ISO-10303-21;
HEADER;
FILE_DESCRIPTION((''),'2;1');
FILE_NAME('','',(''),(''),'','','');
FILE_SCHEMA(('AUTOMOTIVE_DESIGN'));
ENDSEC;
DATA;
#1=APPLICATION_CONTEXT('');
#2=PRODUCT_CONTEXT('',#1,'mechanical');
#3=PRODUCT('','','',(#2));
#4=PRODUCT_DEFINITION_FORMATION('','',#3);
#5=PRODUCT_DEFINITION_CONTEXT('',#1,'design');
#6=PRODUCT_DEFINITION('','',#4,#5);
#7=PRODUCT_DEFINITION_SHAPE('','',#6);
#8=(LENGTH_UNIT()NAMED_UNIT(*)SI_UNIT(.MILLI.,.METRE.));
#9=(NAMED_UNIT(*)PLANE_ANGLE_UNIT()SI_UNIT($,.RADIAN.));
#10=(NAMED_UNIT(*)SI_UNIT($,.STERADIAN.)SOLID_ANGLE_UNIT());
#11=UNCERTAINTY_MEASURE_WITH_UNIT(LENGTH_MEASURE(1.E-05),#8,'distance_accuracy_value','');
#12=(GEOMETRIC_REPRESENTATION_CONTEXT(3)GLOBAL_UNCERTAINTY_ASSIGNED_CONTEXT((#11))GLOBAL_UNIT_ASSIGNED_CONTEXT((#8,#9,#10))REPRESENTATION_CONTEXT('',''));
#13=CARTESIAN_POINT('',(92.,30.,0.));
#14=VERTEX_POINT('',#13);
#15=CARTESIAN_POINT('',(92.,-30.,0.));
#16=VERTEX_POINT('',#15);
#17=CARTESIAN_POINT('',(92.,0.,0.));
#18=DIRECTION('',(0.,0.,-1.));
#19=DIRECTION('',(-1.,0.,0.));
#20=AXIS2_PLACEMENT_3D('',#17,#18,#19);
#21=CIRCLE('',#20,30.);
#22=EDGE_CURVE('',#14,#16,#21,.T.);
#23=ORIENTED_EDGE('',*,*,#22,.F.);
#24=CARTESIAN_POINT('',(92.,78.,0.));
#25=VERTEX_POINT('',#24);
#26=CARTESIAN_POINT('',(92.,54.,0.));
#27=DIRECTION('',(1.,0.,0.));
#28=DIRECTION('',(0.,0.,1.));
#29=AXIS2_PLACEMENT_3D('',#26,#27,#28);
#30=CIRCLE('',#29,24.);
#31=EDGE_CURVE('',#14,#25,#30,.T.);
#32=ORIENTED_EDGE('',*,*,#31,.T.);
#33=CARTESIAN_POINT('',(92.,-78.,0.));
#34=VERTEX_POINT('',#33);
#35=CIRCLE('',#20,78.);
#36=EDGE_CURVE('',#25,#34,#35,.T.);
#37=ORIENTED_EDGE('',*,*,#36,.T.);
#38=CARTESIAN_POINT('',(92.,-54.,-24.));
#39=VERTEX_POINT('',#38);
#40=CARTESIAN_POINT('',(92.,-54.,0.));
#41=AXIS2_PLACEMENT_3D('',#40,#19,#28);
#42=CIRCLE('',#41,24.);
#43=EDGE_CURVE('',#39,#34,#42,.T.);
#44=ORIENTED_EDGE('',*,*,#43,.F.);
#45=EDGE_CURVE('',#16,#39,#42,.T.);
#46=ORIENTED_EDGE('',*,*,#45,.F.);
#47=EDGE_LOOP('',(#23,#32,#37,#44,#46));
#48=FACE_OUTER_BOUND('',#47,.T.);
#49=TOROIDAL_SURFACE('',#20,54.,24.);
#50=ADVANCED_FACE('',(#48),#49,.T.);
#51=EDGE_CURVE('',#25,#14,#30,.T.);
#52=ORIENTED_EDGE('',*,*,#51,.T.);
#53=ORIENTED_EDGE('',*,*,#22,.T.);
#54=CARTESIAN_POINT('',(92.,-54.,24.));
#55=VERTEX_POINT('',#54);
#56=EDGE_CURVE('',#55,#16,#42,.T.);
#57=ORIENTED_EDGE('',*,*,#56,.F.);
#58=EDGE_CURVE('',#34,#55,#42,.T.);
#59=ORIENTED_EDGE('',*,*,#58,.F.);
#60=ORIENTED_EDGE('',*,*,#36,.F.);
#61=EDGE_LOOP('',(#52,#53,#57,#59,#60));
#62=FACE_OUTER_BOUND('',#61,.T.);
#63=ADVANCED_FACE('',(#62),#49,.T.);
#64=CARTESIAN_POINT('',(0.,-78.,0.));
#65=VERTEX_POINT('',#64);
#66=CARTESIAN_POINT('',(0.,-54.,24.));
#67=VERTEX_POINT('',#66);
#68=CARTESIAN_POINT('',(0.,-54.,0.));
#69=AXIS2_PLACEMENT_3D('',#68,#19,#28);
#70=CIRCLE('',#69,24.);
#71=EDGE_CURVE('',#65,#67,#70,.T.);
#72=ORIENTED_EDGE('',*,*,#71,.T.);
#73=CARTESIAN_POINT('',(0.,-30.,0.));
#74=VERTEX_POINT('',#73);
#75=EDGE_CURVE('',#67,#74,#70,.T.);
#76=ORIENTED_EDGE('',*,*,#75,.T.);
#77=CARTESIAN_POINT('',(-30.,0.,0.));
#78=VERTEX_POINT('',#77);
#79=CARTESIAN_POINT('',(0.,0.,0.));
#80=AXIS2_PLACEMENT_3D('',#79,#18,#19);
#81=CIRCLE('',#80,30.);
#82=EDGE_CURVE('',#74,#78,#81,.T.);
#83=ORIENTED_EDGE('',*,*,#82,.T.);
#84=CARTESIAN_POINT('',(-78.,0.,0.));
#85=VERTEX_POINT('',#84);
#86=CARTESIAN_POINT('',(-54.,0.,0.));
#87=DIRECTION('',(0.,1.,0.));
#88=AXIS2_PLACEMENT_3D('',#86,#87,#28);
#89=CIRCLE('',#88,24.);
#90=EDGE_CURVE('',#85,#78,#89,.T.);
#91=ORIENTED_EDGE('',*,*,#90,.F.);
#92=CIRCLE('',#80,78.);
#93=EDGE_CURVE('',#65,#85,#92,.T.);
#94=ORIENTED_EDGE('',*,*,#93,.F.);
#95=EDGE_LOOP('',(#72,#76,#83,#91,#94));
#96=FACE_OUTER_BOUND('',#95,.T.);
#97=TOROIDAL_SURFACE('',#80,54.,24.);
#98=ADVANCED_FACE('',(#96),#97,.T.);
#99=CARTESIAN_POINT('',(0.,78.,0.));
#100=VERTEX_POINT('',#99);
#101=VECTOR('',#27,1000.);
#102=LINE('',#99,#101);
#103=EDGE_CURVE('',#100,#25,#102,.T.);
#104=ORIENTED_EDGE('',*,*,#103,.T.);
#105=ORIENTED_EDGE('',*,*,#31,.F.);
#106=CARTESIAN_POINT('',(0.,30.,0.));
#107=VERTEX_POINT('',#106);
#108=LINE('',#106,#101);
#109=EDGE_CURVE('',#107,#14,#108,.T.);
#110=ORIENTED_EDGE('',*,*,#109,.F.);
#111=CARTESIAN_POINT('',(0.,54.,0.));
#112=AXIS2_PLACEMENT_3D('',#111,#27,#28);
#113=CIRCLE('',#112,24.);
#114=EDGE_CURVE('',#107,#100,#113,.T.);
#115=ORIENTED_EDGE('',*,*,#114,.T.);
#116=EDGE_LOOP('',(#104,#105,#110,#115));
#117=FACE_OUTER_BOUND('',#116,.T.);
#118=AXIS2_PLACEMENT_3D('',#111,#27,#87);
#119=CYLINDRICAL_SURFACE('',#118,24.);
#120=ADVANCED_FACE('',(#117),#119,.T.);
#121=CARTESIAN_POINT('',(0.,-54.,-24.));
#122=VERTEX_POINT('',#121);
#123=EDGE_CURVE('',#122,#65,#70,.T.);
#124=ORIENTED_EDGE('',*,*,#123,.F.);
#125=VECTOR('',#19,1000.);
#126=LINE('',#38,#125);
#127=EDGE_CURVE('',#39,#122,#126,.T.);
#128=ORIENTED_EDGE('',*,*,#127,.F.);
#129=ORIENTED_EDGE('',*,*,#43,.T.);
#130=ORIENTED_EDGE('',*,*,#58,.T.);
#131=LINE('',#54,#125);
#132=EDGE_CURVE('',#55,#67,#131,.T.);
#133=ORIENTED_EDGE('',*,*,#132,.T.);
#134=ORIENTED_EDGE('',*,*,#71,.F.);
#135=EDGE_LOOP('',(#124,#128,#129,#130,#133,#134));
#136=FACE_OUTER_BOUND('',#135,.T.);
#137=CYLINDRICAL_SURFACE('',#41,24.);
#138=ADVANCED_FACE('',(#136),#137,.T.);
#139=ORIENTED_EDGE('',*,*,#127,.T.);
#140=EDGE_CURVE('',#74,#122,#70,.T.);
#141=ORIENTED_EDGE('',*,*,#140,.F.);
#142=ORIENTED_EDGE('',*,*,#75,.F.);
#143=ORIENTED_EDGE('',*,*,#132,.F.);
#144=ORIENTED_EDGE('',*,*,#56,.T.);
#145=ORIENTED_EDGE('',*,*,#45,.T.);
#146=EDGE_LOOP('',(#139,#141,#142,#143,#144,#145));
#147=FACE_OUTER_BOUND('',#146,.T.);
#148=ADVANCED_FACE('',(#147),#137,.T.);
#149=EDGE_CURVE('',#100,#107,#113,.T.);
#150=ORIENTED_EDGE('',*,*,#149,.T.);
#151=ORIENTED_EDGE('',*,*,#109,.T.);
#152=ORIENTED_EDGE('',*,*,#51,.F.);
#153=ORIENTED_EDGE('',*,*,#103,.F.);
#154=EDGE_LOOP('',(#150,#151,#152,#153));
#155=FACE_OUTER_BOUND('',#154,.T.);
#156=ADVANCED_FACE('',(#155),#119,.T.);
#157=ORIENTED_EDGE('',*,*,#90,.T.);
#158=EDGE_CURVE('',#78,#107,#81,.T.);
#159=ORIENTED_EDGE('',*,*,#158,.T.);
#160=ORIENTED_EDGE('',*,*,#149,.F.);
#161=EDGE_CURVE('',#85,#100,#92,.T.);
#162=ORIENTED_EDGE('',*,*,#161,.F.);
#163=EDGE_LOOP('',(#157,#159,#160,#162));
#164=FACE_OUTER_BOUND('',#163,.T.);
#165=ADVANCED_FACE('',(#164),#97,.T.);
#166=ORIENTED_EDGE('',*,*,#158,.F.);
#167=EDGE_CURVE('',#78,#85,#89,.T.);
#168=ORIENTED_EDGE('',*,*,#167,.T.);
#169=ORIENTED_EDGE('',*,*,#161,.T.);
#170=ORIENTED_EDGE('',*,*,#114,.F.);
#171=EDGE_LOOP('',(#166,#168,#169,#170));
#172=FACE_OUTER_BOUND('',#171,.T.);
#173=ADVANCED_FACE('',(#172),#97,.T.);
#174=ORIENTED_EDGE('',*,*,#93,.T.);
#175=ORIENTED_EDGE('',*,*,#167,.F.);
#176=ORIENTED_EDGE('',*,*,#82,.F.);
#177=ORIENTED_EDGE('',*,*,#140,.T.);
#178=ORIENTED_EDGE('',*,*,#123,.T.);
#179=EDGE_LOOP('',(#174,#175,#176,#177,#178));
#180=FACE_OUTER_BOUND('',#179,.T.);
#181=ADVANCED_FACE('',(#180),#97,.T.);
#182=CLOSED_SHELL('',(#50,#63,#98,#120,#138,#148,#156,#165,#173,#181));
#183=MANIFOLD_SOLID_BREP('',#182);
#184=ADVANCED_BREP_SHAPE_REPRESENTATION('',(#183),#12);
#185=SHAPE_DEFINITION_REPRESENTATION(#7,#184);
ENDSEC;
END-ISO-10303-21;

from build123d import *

# Parameters (mm, degrees)
SKETCH_18_R = 24


with BuildPart() as part:
    # 扫描2: sweep along a path in 草图1
    with BuildLine(Plane.XY) as sweep_2_path:
        Line((0, 78), (92, 78))
        ThreePointArc((92, 78), (170, 0), (92, -78))
        Line((92, -78), (0, -78))
        ThreePointArc((0, -78), (-78, 0), (0, 78))
    # 草图18 → 扫描2 (sweep)
    with BuildSketch(Plane(origin=(0, 0, 0), x_dir=(1, 0, 0), z_dir=(0, 1, 0))):
        with Locations((-54, 0)):
            Circle(SKETCH_18_R)
    sweep(path=sweep_2_path.line)


solid = part.part
